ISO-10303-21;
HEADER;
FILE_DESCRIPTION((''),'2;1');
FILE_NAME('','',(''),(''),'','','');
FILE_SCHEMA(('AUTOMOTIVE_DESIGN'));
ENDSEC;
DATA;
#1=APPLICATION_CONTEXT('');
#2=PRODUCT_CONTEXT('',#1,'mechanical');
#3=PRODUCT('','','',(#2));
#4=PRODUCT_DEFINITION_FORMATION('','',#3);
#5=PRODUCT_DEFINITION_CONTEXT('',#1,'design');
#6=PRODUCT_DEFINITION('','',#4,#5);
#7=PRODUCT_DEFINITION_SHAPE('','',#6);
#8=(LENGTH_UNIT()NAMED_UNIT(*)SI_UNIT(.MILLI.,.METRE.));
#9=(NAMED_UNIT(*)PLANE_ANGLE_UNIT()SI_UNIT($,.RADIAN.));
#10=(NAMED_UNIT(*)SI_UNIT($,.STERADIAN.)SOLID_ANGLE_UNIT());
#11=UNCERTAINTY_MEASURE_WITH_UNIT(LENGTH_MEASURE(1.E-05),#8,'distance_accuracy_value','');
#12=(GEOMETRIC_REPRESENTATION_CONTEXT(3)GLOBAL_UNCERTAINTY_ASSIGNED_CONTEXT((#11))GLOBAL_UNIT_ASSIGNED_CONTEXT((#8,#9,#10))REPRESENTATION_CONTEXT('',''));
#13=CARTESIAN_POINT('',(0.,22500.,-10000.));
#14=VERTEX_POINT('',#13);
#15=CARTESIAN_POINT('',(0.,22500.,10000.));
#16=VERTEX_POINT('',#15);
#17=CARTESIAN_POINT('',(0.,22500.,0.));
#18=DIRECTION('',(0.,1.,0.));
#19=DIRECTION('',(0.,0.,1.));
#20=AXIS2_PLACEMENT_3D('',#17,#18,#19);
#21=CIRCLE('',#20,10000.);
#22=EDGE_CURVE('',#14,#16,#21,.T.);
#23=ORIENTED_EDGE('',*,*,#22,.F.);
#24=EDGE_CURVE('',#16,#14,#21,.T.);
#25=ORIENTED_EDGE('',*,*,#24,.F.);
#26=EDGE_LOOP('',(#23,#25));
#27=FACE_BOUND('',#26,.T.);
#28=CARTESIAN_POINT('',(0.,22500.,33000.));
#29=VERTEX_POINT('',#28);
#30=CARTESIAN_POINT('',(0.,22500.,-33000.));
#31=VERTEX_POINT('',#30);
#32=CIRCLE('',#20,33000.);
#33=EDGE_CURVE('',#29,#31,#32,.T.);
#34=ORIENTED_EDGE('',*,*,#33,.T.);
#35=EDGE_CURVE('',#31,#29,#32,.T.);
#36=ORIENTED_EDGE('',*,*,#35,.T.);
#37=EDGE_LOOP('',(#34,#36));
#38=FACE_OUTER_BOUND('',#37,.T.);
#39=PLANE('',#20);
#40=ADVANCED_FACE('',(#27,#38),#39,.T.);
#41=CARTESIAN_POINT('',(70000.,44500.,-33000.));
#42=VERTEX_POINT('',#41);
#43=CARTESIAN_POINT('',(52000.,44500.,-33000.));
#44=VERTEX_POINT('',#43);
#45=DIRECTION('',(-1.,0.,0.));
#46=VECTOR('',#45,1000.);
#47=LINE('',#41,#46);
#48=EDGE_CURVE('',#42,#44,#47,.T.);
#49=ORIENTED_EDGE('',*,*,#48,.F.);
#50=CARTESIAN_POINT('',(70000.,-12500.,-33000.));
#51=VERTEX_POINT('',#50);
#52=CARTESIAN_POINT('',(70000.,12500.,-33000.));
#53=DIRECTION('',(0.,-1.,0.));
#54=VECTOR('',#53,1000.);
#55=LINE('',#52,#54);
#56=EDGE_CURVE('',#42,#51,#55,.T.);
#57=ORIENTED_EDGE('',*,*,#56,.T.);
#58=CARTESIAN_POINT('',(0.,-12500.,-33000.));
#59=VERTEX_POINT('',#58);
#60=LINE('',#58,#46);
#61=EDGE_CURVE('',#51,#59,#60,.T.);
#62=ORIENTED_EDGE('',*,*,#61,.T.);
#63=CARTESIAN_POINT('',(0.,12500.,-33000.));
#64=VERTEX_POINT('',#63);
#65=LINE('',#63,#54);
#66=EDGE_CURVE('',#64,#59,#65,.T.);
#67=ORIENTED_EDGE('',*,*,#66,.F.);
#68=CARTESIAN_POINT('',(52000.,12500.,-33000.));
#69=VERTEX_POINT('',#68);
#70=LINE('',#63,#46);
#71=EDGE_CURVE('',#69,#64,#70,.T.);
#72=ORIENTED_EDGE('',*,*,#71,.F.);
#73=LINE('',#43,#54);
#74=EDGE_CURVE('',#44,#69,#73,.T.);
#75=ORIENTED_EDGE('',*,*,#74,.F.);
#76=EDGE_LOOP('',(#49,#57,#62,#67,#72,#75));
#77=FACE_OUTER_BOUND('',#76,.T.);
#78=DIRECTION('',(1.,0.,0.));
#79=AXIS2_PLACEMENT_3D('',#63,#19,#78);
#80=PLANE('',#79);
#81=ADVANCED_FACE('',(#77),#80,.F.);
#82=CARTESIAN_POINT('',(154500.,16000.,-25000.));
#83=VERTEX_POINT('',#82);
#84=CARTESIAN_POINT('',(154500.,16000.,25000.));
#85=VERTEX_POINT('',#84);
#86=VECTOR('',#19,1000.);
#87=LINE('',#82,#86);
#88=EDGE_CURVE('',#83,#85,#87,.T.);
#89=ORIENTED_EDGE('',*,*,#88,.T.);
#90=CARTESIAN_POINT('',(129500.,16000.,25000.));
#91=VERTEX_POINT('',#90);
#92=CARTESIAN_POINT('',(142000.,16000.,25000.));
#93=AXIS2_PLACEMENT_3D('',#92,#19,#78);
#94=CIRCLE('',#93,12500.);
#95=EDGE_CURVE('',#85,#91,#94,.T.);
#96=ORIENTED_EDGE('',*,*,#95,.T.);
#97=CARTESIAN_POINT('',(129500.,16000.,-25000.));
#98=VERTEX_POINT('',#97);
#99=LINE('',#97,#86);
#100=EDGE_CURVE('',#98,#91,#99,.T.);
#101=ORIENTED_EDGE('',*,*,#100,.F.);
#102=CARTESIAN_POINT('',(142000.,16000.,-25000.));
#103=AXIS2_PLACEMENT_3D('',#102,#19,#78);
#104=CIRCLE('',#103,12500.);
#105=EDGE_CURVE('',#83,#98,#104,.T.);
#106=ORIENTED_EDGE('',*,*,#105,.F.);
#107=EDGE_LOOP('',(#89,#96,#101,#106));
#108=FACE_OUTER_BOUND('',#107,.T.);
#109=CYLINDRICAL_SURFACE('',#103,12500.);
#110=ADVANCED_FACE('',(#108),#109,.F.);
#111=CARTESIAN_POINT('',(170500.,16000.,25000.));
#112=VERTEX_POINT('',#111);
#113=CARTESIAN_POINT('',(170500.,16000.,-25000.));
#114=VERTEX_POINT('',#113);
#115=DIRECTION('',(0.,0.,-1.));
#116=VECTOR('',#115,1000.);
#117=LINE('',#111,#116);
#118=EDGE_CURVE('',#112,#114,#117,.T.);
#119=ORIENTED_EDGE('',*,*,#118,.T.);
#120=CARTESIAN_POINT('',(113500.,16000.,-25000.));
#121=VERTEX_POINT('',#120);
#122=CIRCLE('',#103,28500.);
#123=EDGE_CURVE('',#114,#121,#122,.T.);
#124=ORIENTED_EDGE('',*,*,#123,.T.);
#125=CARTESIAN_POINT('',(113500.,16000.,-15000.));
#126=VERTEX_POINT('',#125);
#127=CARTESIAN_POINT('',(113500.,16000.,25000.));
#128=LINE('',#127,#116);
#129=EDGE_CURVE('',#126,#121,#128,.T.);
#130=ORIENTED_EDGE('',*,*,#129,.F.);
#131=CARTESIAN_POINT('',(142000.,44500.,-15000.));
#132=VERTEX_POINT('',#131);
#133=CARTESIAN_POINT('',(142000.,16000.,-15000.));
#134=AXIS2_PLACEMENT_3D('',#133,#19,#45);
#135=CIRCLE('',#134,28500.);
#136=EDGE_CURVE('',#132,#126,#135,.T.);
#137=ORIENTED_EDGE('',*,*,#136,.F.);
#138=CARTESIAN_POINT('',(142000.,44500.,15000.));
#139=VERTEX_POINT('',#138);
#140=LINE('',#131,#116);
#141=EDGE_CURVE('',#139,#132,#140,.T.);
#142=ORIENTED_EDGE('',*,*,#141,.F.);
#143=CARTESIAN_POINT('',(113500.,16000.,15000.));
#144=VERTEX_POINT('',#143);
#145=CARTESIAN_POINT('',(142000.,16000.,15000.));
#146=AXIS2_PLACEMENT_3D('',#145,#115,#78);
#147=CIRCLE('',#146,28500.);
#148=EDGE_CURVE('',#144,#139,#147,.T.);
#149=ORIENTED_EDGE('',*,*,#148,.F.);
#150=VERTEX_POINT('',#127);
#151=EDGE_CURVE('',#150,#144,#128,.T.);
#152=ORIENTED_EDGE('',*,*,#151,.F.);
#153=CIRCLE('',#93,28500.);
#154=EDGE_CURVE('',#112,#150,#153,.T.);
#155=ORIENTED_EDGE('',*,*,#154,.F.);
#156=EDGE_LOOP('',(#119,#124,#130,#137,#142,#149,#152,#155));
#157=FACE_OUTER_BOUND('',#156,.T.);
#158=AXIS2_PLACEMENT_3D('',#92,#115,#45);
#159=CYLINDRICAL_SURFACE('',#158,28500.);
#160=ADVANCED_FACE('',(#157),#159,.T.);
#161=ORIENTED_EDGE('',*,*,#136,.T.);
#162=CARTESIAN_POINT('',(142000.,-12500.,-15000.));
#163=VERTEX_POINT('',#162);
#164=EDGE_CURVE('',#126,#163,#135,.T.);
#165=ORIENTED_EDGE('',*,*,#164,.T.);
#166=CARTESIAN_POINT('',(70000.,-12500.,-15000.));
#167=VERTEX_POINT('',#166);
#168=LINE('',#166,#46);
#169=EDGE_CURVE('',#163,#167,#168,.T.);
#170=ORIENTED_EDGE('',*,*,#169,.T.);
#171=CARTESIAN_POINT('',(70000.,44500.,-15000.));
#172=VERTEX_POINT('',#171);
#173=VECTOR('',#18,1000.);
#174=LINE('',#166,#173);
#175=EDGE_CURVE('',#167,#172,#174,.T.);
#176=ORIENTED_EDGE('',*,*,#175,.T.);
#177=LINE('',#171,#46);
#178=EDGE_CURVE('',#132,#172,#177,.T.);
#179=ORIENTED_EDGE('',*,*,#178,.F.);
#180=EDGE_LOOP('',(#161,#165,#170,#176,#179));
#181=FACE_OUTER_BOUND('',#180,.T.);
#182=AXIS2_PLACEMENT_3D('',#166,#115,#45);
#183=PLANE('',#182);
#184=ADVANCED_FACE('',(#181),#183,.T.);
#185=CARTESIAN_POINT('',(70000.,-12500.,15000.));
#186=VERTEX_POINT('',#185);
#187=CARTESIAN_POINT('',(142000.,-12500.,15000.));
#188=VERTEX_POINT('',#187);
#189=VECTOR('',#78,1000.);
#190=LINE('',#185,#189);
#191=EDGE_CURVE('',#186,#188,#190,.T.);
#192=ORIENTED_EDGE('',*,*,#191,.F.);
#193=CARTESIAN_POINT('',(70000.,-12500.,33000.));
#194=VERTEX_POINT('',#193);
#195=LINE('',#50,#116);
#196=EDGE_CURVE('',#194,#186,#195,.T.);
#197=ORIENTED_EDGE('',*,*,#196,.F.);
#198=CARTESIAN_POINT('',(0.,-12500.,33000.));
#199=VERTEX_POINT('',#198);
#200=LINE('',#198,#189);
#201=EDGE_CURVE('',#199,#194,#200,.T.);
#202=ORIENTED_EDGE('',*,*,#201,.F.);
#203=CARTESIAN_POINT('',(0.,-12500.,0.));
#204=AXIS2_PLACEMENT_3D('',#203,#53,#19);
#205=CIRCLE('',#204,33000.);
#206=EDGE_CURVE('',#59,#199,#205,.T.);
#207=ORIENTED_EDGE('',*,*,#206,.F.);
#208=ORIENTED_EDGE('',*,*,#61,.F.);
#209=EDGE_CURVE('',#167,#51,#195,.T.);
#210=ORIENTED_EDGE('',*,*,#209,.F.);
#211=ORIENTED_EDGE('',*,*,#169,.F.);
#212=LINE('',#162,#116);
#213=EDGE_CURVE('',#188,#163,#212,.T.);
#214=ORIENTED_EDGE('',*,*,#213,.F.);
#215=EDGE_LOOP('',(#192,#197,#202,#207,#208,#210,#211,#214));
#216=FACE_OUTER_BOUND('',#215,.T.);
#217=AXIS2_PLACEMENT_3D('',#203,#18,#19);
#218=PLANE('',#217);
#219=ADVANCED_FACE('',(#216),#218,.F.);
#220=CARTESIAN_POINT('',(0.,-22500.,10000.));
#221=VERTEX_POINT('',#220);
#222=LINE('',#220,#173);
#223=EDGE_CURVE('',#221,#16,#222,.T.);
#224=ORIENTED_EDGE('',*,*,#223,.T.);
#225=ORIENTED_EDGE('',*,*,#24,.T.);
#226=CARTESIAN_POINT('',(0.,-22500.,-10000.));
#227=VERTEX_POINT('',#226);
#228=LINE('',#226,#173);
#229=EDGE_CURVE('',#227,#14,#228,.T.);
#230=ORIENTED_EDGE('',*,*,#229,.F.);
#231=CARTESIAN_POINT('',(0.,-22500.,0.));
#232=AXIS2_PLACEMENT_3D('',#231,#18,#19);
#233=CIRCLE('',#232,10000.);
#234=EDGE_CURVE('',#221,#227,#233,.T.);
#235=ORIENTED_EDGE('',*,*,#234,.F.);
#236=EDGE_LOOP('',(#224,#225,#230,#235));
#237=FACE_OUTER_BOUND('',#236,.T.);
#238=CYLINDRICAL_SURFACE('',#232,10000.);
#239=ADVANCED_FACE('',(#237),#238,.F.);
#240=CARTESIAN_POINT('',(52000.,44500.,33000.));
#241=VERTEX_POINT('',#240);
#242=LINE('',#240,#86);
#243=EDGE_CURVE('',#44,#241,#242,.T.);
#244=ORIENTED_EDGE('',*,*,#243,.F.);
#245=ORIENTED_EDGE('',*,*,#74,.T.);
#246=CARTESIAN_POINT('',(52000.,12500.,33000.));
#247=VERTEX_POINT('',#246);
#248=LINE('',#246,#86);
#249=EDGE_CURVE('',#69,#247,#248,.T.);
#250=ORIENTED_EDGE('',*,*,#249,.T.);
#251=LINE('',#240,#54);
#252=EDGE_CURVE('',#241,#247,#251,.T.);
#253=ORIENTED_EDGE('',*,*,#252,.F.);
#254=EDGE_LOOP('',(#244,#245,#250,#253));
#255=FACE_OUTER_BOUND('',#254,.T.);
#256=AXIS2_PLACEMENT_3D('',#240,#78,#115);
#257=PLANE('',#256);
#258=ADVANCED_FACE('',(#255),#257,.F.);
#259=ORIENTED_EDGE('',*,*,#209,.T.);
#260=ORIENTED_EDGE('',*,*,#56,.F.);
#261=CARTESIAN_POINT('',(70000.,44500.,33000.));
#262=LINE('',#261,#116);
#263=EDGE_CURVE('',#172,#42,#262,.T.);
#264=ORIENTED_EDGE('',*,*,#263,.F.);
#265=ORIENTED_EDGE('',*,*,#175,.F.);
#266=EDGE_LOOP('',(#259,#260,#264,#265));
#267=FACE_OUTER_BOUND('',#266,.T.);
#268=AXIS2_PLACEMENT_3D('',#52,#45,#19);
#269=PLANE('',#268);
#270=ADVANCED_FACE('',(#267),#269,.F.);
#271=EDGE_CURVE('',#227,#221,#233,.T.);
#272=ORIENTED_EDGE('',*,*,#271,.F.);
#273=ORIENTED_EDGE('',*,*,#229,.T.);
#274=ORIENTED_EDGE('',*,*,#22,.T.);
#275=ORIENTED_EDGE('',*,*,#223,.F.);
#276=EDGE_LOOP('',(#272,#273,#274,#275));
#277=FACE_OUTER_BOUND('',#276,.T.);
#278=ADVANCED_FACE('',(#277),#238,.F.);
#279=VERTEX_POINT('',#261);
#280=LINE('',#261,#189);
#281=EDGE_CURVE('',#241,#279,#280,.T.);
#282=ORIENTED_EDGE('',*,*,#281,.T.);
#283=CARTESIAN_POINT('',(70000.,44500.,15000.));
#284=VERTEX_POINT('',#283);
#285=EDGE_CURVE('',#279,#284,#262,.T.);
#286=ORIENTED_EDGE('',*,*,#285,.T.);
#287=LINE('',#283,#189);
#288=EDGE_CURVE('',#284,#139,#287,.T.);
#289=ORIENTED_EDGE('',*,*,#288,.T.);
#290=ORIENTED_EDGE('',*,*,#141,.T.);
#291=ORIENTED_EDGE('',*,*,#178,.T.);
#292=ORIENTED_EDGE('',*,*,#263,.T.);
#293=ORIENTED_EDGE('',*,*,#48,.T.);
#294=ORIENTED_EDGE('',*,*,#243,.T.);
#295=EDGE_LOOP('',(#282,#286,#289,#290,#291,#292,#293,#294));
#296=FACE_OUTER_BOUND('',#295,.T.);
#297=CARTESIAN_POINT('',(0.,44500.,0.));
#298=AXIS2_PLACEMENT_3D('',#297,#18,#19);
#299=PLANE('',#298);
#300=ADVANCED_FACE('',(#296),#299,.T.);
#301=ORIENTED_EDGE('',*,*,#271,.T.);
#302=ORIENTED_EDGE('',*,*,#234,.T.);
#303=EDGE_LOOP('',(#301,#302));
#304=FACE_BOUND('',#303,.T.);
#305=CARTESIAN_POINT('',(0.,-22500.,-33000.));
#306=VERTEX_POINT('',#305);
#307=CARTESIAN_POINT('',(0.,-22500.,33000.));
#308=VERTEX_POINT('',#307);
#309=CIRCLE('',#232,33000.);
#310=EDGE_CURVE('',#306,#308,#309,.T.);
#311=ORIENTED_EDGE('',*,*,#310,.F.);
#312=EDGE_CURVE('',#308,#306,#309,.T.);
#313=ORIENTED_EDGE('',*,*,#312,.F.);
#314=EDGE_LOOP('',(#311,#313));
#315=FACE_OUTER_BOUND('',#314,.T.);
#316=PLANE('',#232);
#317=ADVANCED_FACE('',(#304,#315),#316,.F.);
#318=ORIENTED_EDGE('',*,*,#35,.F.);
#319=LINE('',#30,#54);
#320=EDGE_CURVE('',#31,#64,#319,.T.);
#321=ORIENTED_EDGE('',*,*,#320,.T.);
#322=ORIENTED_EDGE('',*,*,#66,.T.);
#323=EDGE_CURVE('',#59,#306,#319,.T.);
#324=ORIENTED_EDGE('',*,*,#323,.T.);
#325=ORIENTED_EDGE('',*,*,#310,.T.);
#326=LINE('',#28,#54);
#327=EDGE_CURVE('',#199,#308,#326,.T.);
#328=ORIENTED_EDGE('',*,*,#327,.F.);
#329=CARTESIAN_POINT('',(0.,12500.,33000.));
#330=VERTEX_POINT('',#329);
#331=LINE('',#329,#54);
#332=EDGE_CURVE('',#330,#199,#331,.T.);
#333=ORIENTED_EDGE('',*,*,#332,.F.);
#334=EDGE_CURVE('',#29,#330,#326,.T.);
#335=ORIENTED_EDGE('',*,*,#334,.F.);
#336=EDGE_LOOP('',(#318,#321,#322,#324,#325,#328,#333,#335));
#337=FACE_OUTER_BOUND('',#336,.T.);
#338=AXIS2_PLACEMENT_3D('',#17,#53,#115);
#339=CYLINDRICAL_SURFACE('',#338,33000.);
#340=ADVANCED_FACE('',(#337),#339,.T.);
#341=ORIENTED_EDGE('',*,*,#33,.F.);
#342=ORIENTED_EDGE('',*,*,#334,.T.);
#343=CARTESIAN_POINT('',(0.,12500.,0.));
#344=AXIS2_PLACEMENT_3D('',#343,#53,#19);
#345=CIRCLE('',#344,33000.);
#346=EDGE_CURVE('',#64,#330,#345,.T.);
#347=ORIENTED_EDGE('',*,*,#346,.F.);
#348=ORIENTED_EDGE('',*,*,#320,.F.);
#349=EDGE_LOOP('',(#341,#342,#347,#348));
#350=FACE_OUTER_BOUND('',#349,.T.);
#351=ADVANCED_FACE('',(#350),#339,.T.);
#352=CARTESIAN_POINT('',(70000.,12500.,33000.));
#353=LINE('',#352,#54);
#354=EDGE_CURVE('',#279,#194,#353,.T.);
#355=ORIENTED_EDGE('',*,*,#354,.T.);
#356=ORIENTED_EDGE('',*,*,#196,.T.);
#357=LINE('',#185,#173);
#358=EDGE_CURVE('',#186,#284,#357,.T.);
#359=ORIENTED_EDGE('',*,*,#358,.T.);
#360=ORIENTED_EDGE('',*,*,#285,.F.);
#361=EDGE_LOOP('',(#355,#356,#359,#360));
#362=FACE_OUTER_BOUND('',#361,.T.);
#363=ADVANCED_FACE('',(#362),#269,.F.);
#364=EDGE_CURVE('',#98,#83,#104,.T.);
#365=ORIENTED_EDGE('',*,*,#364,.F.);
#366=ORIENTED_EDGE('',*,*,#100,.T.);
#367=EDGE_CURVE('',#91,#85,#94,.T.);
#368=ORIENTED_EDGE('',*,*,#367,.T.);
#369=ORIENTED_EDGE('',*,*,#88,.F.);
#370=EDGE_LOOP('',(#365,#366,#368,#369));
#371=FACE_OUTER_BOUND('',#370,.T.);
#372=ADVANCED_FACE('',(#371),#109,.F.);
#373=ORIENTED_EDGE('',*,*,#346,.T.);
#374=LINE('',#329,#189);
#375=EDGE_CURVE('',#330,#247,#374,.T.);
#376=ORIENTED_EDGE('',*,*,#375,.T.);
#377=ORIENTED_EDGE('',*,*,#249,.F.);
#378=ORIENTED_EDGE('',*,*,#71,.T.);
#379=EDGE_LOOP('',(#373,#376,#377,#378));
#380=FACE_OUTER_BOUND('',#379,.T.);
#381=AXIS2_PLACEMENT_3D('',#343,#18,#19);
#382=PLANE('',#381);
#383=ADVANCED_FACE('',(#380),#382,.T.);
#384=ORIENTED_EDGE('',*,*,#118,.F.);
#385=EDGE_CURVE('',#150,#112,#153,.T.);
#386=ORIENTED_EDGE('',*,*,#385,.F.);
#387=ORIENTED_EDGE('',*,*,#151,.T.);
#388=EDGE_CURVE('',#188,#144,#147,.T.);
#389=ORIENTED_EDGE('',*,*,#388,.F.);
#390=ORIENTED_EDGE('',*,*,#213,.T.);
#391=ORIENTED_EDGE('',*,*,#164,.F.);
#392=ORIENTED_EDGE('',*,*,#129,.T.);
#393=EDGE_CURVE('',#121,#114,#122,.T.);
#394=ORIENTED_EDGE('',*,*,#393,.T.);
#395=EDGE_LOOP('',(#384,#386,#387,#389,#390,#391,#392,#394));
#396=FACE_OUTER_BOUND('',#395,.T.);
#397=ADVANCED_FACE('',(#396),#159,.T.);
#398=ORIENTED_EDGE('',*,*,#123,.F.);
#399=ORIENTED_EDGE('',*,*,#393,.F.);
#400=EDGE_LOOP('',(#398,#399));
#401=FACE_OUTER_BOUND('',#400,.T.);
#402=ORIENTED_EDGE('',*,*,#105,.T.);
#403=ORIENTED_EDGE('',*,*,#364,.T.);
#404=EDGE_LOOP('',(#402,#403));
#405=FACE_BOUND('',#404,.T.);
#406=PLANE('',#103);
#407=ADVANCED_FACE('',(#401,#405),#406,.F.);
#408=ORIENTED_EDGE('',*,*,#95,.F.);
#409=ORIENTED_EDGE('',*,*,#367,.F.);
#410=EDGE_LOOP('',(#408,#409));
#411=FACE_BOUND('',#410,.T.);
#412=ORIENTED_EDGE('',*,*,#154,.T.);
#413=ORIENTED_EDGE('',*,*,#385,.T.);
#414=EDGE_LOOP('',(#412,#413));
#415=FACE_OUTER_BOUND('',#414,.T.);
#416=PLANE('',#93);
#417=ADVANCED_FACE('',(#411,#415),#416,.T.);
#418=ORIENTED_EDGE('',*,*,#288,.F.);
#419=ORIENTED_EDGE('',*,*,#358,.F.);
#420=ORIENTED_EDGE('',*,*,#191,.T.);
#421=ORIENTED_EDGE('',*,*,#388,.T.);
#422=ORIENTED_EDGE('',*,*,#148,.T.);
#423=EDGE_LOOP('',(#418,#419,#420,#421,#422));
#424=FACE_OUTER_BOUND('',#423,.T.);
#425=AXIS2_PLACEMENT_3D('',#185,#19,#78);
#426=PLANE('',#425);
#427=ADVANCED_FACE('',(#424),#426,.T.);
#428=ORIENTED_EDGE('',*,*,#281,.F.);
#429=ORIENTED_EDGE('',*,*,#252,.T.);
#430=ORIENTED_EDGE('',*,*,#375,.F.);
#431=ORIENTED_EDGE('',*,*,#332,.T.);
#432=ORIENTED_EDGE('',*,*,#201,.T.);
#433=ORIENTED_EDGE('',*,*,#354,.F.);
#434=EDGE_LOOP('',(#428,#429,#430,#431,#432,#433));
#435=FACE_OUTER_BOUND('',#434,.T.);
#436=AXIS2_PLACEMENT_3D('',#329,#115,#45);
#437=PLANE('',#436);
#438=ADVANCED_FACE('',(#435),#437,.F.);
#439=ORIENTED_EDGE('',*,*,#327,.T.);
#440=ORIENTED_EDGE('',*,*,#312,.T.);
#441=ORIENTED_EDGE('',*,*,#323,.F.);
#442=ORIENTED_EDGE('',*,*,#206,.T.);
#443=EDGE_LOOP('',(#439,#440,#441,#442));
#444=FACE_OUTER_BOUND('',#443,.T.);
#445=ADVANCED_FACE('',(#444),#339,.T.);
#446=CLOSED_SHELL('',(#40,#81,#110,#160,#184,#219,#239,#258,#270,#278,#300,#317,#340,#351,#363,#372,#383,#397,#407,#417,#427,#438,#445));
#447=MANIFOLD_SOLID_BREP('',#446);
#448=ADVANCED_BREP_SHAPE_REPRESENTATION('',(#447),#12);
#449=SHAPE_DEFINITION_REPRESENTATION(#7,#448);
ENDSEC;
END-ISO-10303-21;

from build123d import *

# Parameters (mm, degrees)
VERTICAL_EYE_BOSS_SKETCH_66_R   = 33000
VERTICAL_EYE_BOSS_66_DEPTH      = 22500
VERTICAL_EYE_BORE_SKETCH_20_R   = 10000
VERTICAL_EYE_BORE_20_DEPTH      = 45000
ARM_BASE_PLATE_DEPTH            = 12500
ARM_WEB_SKETCH_W                = 18000
ARM_WEB_SKETCH_H                = 66000
ARM_WEB_DEPTH                   = 32000
ARM_RIB_PROFILE_SKETCH_W        = 72000
ARM_RIB_PROFILE_SKETCH_H        = 30000
ARM_RIB_DEPTH                   = 57000
HORIZONTAL_EYE_BOSS_SKETCH_R    = 28500
HORIZONTAL_EYE_BOSS_DEPTH       = 25000
HORIZONTAL_EYE_BORE_SKETCH_25_R = 12500
HORIZONTAL_EYE_BORE_25_DEPTH    = 50000


with BuildPart() as part:
    # Vertical Eye Boss Sketch Ø66 → Vertical Eye Boss Ø66 (new, symmetric)
    with BuildSketch(Plane(origin=(0, 0, 0), x_dir=(1, 0, 0), z_dir=(0, 1, 0))):
        with Locations(Location((0, 0, 0), (0, 0, 270))):
            Circle(VERTICAL_EYE_BOSS_SKETCH_66_R)
    extrude(amount=VERTICAL_EYE_BOSS_66_DEPTH, both=True)

    # Vertical Eye Bore Sketch Ø20 → Vertical Eye Bore Ø20 (cut)
    with BuildSketch(Plane(origin=(0, 22500, 0), x_dir=(1, 0, 0), z_dir=(0, 1, 0))):
        with Locations(Location((0, 0, 0), (0, 0, 270))):
            Circle(VERTICAL_EYE_BORE_SKETCH_20_R)
    extrude(amount=-VERTICAL_EYE_BORE_20_DEPTH, mode=Mode.SUBTRACT)

    # Arm Base Sketch → Arm Base Plate (add, symmetric)
    with BuildSketch(Plane(origin=(0, 0, 0), x_dir=(1, 0, 0), z_dir=(0, 1, 0))):
        with BuildLine():
            Line((0, 33000), (70000, 33000))
            Line((70000, 33000), (70000, -33000))
            Line((70000, -33000), (0, -33000))
            ThreePointArc((0, -33000), (33000, 0), (0, 33000))
        make_face()
    extrude(amount=ARM_BASE_PLATE_DEPTH, both=True)

    # Arm Web Sketch → Arm Web (add)
    with BuildSketch(Plane(origin=(0, 12500, 0), x_dir=(1, 0, 0), z_dir=(0, 1, 0))):
        with Locations((61000, 0)):
            Rectangle(ARM_WEB_SKETCH_W, ARM_WEB_SKETCH_H)
    extrude(amount=ARM_WEB_DEPTH)

    # Arm Rib Profile Sketch → Arm Rib (add)
    with BuildSketch(Plane(origin=(0, 44500, 0), x_dir=(1, 0, 0), z_dir=(0, 1, 0))):
        with Locations((106000, 0)):
            Rectangle(ARM_RIB_PROFILE_SKETCH_W, ARM_RIB_PROFILE_SKETCH_H)
    extrude(amount=-ARM_RIB_DEPTH)

    # Horizontal Eye Boss Sketch → Horizontal Eye Boss (add, symmetric)
    with BuildSketch(Plane.XY):
        with Locations((142000, 16000)):
            Circle(HORIZONTAL_EYE_BOSS_SKETCH_R)
    extrude(amount=HORIZONTAL_EYE_BOSS_DEPTH, both=True)

    # Horizontal Eye Bore Sketch Ø25 → Horizontal Eye Bore Ø25 (cut)
    with BuildSketch(Plane.XY.offset(25000)):
        with Locations((142000, 16000)):
            Circle(HORIZONTAL_EYE_BORE_SKETCH_25_R)
    extrude(amount=-HORIZONTAL_EYE_BORE_25_DEPTH, mode=Mode.SUBTRACT)


solid = part.part
